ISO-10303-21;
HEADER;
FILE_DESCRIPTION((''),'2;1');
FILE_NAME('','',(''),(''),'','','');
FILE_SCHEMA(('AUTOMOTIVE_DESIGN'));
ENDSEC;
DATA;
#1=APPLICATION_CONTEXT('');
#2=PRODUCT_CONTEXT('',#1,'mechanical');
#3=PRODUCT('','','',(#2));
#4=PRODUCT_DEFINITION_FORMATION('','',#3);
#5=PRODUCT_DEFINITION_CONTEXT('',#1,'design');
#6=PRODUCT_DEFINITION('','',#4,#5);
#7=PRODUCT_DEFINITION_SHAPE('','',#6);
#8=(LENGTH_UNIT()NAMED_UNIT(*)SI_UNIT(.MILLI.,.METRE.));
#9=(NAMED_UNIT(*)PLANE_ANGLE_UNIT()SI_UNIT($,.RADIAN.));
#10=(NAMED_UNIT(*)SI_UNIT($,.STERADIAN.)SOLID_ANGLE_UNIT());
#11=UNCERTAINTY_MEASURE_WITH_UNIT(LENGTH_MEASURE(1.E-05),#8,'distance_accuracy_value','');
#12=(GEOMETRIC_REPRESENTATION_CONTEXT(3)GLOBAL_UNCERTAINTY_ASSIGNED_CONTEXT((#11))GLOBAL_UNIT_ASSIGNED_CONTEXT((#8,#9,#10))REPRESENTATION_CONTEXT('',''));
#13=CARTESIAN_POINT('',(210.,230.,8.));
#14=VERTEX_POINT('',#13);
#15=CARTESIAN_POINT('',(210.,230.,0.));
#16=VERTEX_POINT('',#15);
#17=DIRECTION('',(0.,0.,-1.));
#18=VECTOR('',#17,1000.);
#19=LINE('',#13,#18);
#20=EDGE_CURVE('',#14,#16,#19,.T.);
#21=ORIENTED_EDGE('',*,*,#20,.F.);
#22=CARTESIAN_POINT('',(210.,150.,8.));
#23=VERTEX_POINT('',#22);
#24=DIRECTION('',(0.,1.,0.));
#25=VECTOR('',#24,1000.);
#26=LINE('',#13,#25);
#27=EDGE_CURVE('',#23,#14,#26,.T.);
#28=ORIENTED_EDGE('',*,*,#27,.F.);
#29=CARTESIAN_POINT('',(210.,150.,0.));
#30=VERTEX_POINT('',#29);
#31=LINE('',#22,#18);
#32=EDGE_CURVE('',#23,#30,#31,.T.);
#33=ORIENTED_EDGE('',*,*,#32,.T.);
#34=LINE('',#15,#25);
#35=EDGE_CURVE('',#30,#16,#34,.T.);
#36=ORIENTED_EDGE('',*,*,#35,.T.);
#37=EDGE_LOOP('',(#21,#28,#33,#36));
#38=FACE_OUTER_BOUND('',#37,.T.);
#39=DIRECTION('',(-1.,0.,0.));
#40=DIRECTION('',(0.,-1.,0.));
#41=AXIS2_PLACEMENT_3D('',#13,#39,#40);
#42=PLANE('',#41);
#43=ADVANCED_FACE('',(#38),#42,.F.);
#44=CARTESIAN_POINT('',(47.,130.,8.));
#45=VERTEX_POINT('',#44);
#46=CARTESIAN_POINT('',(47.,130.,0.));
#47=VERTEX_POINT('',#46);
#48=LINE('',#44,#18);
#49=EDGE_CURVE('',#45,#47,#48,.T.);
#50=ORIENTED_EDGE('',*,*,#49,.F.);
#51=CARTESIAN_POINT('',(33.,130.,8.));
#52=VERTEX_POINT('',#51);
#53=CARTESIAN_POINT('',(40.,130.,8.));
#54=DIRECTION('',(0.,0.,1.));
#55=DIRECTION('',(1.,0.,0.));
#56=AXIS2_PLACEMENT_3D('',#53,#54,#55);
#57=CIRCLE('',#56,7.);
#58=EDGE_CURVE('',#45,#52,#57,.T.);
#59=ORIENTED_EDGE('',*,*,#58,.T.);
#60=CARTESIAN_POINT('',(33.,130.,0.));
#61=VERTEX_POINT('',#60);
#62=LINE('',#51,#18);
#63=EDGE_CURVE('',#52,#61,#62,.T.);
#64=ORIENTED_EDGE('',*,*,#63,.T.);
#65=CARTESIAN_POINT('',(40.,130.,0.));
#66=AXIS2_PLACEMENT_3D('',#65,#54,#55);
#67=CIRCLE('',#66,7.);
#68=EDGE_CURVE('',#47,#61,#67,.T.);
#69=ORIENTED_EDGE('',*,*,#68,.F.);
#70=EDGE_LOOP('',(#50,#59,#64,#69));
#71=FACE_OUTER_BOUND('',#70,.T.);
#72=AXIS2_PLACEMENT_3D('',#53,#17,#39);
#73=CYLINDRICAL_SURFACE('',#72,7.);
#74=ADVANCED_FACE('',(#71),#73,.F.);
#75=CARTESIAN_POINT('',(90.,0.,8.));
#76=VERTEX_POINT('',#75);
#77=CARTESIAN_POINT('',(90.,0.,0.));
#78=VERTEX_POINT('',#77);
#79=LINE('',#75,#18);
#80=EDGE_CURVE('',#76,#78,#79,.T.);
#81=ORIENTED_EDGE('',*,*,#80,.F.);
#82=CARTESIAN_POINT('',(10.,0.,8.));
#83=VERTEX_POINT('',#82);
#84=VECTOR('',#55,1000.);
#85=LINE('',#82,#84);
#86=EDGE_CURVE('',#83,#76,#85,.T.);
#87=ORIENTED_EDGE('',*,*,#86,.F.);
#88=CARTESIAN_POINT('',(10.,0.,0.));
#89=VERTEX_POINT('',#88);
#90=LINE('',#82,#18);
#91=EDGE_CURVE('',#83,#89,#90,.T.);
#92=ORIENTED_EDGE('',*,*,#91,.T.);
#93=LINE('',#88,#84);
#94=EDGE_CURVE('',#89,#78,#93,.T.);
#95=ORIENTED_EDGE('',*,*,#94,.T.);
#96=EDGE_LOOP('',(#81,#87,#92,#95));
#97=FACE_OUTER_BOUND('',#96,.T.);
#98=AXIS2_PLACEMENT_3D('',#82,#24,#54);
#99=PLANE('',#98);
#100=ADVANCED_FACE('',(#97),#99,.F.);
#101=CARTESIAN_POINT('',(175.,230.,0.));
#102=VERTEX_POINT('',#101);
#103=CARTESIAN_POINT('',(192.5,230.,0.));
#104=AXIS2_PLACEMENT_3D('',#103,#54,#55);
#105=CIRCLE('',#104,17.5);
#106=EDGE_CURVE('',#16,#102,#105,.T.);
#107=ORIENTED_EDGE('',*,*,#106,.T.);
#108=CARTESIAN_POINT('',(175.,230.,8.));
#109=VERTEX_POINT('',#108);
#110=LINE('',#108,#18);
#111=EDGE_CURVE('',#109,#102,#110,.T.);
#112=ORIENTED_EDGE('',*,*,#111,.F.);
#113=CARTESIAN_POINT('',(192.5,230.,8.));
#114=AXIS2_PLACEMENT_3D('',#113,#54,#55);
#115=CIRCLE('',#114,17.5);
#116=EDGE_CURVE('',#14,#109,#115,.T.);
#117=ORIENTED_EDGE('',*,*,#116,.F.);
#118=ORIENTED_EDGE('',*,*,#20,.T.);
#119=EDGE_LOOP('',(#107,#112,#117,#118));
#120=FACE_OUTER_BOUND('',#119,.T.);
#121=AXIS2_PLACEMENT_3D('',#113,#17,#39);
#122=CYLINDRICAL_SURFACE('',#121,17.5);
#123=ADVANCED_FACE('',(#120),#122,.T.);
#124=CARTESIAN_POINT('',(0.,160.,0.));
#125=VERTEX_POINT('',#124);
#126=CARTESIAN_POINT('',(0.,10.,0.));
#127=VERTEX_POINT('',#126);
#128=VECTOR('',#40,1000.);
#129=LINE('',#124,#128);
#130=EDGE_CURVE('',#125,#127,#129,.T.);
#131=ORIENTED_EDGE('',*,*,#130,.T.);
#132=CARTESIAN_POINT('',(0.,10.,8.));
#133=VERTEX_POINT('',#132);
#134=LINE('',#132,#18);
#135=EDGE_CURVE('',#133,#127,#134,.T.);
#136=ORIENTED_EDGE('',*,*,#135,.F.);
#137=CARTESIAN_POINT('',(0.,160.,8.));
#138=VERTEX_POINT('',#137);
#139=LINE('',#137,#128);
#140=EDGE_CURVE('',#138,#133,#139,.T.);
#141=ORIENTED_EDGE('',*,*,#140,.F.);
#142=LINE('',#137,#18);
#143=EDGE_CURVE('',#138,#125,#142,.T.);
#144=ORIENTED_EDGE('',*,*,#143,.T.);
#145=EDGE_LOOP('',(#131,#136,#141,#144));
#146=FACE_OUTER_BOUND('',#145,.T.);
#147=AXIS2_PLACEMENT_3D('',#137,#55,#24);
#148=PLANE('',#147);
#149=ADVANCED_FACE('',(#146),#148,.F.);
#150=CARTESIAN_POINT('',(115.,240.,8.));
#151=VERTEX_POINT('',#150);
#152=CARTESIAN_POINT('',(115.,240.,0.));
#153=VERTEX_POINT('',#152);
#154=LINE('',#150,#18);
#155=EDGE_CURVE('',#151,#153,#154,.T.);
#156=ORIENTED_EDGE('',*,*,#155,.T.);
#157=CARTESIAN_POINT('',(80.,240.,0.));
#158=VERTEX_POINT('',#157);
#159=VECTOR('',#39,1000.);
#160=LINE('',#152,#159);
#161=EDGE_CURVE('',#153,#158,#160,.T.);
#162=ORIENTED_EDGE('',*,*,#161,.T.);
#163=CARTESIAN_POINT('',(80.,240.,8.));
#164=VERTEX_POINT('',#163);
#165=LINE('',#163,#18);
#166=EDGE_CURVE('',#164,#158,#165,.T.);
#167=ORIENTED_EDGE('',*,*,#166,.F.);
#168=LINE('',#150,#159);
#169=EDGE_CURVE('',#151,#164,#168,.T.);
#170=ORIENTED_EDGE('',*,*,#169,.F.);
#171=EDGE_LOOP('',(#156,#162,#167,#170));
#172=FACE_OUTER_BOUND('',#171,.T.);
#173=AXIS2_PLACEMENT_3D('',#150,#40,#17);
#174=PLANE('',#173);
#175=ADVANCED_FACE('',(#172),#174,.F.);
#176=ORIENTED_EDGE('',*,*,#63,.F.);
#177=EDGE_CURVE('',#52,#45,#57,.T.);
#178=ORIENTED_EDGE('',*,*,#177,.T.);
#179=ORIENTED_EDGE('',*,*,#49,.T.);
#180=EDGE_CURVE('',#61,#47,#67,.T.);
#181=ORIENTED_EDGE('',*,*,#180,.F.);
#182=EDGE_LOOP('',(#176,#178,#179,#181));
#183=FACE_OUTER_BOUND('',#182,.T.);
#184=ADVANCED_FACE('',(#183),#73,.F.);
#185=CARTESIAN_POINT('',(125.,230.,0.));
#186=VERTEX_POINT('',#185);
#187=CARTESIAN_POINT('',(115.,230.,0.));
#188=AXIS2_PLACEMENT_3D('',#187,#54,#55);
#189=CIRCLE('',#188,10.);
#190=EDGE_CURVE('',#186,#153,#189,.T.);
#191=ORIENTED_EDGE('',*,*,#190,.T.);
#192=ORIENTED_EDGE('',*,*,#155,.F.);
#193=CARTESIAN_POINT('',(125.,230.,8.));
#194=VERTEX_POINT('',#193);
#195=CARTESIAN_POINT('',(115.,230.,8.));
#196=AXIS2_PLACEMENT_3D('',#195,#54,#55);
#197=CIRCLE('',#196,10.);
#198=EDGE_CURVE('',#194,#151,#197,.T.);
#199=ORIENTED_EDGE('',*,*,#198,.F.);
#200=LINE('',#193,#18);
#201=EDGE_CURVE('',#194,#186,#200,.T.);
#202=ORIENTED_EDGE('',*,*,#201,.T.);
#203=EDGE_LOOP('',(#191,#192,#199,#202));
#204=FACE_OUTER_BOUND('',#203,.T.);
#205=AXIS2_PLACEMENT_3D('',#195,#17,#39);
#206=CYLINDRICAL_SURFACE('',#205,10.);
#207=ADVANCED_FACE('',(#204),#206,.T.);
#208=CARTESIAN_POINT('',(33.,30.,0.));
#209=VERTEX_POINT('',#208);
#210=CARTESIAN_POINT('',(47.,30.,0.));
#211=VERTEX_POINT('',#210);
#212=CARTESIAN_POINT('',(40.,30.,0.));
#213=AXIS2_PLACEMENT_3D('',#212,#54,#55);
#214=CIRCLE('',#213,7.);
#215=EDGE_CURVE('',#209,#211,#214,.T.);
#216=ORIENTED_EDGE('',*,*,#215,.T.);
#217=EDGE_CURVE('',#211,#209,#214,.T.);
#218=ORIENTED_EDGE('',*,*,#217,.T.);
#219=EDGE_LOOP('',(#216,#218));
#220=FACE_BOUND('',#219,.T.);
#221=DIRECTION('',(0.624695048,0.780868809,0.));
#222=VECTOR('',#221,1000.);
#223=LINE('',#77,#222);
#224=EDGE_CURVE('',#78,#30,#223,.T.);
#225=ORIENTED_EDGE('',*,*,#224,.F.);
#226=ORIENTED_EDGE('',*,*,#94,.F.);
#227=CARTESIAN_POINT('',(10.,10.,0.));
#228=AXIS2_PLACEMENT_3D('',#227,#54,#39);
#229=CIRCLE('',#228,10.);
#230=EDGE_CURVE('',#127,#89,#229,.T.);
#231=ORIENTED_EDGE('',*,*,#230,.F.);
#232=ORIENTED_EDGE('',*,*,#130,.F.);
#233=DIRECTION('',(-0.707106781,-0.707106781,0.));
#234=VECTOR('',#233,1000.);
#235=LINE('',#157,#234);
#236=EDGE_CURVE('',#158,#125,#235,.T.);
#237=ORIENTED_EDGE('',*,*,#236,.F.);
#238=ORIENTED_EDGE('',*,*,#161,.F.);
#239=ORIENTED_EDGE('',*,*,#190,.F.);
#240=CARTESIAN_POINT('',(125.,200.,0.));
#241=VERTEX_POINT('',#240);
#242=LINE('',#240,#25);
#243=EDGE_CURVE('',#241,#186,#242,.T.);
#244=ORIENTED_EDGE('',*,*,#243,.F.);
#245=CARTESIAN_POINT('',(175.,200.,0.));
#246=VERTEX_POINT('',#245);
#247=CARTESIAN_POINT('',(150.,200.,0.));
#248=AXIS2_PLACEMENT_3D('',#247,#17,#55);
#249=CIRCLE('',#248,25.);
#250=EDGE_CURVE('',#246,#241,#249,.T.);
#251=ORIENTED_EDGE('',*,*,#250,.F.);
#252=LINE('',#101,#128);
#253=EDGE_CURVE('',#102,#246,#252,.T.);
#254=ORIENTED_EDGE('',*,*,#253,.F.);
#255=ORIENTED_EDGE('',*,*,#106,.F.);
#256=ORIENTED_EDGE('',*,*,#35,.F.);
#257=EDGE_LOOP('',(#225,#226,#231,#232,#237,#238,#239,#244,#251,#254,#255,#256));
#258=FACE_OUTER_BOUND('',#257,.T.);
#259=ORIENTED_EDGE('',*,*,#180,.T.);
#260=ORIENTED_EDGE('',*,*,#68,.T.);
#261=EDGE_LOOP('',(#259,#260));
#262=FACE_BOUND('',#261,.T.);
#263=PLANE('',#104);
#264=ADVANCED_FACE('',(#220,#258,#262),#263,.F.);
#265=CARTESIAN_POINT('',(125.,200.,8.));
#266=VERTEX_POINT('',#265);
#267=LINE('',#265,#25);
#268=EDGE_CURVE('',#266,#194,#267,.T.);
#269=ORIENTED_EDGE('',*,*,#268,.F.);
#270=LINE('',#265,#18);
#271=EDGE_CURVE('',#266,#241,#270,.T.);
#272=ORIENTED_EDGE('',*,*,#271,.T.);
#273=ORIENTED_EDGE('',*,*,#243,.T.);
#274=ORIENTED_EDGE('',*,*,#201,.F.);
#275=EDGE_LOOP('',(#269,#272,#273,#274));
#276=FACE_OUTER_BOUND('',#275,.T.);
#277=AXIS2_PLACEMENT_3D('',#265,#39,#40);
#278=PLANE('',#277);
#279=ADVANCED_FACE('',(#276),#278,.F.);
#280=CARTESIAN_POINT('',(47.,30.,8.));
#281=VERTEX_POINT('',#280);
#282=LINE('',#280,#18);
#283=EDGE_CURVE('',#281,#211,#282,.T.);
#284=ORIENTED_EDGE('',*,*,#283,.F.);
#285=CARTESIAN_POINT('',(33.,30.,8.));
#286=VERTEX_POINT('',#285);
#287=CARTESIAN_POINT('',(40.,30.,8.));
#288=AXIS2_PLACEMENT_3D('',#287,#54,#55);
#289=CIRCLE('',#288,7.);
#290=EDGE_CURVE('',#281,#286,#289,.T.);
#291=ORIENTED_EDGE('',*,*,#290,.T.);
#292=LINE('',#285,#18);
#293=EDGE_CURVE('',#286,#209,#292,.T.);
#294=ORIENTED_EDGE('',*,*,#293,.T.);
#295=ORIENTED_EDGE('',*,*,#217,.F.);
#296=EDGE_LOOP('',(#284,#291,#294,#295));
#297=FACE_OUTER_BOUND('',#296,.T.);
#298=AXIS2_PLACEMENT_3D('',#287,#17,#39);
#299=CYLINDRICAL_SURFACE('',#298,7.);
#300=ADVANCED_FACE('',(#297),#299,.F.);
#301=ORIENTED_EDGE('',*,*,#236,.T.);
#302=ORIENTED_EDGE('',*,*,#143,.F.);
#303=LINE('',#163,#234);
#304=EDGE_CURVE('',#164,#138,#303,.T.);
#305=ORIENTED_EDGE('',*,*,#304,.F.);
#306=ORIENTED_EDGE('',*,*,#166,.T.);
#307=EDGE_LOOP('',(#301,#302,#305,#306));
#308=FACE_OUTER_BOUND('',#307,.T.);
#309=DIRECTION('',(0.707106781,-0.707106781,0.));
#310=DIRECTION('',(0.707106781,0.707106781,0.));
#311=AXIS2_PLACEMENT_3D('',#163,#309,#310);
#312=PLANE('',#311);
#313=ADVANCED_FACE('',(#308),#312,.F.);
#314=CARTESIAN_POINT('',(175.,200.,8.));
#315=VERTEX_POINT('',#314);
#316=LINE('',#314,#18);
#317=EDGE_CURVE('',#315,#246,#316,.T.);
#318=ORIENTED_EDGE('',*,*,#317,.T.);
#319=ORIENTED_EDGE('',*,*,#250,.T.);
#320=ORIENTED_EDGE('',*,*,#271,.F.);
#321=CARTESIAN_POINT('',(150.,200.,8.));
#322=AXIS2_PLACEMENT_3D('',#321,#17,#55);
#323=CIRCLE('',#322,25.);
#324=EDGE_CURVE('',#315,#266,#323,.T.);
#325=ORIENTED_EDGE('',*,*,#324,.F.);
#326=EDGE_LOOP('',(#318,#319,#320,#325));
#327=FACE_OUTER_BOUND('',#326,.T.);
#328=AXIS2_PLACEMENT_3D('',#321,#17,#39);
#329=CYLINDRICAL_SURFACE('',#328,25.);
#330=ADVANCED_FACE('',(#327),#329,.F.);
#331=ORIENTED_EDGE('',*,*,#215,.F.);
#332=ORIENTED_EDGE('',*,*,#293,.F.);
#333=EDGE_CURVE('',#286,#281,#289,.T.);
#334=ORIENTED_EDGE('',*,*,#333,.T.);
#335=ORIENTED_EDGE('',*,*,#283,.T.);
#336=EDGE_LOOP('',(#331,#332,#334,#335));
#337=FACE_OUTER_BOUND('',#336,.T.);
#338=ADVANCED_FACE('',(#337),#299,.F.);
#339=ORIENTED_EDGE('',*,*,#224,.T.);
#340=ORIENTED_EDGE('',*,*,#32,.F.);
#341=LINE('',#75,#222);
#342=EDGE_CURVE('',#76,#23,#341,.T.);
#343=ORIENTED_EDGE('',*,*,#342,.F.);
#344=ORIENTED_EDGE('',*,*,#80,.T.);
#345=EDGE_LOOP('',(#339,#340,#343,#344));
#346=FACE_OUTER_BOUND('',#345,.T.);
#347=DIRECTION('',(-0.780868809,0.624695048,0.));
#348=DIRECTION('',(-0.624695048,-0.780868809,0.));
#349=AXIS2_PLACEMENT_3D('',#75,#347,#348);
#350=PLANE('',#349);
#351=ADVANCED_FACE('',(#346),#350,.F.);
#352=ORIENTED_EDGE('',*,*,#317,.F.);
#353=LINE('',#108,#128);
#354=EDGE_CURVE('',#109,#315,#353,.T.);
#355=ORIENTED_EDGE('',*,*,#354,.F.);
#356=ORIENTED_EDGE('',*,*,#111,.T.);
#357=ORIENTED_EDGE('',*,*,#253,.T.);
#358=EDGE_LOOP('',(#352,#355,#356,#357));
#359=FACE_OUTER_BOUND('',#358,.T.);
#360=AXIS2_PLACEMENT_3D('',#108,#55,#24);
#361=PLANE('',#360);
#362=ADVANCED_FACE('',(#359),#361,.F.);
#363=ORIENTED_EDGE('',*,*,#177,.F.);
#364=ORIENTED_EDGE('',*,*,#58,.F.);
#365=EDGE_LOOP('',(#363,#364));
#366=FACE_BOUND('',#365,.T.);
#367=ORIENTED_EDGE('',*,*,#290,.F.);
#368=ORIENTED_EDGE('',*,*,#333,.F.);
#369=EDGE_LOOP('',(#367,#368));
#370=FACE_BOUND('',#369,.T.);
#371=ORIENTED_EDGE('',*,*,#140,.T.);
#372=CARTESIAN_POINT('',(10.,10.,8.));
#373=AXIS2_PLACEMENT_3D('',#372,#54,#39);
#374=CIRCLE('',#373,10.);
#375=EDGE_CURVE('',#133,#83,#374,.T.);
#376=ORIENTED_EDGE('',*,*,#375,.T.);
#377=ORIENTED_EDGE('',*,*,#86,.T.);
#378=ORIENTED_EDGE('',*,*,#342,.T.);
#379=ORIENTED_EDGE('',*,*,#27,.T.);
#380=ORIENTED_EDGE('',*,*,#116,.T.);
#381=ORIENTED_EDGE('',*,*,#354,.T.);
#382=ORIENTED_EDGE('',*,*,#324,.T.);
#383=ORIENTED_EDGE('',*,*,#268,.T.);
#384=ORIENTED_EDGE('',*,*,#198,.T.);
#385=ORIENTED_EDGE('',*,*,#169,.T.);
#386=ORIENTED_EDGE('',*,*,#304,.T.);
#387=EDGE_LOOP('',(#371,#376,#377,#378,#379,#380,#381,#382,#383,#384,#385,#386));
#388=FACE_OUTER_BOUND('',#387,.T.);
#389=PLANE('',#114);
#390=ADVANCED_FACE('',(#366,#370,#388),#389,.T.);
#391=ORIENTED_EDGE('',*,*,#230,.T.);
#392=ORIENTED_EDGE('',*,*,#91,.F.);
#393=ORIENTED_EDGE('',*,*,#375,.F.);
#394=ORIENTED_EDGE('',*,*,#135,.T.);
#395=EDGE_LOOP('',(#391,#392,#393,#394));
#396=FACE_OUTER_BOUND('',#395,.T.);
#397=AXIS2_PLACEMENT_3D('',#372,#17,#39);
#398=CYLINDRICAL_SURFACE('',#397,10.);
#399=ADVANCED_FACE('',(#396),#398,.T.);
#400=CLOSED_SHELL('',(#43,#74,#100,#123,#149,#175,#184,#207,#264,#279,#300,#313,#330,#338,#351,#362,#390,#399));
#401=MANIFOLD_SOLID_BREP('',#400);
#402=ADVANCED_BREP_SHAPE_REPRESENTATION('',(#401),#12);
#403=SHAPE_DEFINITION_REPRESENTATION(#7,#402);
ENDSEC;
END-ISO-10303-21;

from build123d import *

# Parameters (mm, degrees)
SKETCH1_R           = 7
BOSS_EXTRUDE1_DEPTH = 8


with BuildPart() as part:
    # Sketch1 → Boss-Extrude1 (new body)
    with BuildSketch(Plane.XY):
        with BuildLine():
            Line((10, 0), (90, 0))
            Line((90, 0), (210, 150))
            Line((210, 150), (210, 230))
            ThreePointArc((210, 230), (192.5, 247.5), (175, 230))
            Line((175, 230), (175, 200))
            ThreePointArc((175, 200), (150, 175), (125, 200))
            Line((125, 200), (125, 230))
            ThreePointArc((125, 230), (122.071067812, 237.071067812), (115, 240))
            Line((115, 240), (80, 240))
            Line((80, 240), (0, 160))
            Line((0, 160), (0, 10))
            ThreePointArc((0, 10), (2.928932188, 2.928932188), (10, 0))
        make_face()
        with Locations((40, 130)):
            Circle(SKETCH1_R, mode=Mode.SUBTRACT)
        with Locations((40, 30)):
            Circle(SKETCH1_R, mode=Mode.SUBTRACT)
    extrude(amount=BOSS_EXTRUDE1_DEPTH)


solid = part.part
